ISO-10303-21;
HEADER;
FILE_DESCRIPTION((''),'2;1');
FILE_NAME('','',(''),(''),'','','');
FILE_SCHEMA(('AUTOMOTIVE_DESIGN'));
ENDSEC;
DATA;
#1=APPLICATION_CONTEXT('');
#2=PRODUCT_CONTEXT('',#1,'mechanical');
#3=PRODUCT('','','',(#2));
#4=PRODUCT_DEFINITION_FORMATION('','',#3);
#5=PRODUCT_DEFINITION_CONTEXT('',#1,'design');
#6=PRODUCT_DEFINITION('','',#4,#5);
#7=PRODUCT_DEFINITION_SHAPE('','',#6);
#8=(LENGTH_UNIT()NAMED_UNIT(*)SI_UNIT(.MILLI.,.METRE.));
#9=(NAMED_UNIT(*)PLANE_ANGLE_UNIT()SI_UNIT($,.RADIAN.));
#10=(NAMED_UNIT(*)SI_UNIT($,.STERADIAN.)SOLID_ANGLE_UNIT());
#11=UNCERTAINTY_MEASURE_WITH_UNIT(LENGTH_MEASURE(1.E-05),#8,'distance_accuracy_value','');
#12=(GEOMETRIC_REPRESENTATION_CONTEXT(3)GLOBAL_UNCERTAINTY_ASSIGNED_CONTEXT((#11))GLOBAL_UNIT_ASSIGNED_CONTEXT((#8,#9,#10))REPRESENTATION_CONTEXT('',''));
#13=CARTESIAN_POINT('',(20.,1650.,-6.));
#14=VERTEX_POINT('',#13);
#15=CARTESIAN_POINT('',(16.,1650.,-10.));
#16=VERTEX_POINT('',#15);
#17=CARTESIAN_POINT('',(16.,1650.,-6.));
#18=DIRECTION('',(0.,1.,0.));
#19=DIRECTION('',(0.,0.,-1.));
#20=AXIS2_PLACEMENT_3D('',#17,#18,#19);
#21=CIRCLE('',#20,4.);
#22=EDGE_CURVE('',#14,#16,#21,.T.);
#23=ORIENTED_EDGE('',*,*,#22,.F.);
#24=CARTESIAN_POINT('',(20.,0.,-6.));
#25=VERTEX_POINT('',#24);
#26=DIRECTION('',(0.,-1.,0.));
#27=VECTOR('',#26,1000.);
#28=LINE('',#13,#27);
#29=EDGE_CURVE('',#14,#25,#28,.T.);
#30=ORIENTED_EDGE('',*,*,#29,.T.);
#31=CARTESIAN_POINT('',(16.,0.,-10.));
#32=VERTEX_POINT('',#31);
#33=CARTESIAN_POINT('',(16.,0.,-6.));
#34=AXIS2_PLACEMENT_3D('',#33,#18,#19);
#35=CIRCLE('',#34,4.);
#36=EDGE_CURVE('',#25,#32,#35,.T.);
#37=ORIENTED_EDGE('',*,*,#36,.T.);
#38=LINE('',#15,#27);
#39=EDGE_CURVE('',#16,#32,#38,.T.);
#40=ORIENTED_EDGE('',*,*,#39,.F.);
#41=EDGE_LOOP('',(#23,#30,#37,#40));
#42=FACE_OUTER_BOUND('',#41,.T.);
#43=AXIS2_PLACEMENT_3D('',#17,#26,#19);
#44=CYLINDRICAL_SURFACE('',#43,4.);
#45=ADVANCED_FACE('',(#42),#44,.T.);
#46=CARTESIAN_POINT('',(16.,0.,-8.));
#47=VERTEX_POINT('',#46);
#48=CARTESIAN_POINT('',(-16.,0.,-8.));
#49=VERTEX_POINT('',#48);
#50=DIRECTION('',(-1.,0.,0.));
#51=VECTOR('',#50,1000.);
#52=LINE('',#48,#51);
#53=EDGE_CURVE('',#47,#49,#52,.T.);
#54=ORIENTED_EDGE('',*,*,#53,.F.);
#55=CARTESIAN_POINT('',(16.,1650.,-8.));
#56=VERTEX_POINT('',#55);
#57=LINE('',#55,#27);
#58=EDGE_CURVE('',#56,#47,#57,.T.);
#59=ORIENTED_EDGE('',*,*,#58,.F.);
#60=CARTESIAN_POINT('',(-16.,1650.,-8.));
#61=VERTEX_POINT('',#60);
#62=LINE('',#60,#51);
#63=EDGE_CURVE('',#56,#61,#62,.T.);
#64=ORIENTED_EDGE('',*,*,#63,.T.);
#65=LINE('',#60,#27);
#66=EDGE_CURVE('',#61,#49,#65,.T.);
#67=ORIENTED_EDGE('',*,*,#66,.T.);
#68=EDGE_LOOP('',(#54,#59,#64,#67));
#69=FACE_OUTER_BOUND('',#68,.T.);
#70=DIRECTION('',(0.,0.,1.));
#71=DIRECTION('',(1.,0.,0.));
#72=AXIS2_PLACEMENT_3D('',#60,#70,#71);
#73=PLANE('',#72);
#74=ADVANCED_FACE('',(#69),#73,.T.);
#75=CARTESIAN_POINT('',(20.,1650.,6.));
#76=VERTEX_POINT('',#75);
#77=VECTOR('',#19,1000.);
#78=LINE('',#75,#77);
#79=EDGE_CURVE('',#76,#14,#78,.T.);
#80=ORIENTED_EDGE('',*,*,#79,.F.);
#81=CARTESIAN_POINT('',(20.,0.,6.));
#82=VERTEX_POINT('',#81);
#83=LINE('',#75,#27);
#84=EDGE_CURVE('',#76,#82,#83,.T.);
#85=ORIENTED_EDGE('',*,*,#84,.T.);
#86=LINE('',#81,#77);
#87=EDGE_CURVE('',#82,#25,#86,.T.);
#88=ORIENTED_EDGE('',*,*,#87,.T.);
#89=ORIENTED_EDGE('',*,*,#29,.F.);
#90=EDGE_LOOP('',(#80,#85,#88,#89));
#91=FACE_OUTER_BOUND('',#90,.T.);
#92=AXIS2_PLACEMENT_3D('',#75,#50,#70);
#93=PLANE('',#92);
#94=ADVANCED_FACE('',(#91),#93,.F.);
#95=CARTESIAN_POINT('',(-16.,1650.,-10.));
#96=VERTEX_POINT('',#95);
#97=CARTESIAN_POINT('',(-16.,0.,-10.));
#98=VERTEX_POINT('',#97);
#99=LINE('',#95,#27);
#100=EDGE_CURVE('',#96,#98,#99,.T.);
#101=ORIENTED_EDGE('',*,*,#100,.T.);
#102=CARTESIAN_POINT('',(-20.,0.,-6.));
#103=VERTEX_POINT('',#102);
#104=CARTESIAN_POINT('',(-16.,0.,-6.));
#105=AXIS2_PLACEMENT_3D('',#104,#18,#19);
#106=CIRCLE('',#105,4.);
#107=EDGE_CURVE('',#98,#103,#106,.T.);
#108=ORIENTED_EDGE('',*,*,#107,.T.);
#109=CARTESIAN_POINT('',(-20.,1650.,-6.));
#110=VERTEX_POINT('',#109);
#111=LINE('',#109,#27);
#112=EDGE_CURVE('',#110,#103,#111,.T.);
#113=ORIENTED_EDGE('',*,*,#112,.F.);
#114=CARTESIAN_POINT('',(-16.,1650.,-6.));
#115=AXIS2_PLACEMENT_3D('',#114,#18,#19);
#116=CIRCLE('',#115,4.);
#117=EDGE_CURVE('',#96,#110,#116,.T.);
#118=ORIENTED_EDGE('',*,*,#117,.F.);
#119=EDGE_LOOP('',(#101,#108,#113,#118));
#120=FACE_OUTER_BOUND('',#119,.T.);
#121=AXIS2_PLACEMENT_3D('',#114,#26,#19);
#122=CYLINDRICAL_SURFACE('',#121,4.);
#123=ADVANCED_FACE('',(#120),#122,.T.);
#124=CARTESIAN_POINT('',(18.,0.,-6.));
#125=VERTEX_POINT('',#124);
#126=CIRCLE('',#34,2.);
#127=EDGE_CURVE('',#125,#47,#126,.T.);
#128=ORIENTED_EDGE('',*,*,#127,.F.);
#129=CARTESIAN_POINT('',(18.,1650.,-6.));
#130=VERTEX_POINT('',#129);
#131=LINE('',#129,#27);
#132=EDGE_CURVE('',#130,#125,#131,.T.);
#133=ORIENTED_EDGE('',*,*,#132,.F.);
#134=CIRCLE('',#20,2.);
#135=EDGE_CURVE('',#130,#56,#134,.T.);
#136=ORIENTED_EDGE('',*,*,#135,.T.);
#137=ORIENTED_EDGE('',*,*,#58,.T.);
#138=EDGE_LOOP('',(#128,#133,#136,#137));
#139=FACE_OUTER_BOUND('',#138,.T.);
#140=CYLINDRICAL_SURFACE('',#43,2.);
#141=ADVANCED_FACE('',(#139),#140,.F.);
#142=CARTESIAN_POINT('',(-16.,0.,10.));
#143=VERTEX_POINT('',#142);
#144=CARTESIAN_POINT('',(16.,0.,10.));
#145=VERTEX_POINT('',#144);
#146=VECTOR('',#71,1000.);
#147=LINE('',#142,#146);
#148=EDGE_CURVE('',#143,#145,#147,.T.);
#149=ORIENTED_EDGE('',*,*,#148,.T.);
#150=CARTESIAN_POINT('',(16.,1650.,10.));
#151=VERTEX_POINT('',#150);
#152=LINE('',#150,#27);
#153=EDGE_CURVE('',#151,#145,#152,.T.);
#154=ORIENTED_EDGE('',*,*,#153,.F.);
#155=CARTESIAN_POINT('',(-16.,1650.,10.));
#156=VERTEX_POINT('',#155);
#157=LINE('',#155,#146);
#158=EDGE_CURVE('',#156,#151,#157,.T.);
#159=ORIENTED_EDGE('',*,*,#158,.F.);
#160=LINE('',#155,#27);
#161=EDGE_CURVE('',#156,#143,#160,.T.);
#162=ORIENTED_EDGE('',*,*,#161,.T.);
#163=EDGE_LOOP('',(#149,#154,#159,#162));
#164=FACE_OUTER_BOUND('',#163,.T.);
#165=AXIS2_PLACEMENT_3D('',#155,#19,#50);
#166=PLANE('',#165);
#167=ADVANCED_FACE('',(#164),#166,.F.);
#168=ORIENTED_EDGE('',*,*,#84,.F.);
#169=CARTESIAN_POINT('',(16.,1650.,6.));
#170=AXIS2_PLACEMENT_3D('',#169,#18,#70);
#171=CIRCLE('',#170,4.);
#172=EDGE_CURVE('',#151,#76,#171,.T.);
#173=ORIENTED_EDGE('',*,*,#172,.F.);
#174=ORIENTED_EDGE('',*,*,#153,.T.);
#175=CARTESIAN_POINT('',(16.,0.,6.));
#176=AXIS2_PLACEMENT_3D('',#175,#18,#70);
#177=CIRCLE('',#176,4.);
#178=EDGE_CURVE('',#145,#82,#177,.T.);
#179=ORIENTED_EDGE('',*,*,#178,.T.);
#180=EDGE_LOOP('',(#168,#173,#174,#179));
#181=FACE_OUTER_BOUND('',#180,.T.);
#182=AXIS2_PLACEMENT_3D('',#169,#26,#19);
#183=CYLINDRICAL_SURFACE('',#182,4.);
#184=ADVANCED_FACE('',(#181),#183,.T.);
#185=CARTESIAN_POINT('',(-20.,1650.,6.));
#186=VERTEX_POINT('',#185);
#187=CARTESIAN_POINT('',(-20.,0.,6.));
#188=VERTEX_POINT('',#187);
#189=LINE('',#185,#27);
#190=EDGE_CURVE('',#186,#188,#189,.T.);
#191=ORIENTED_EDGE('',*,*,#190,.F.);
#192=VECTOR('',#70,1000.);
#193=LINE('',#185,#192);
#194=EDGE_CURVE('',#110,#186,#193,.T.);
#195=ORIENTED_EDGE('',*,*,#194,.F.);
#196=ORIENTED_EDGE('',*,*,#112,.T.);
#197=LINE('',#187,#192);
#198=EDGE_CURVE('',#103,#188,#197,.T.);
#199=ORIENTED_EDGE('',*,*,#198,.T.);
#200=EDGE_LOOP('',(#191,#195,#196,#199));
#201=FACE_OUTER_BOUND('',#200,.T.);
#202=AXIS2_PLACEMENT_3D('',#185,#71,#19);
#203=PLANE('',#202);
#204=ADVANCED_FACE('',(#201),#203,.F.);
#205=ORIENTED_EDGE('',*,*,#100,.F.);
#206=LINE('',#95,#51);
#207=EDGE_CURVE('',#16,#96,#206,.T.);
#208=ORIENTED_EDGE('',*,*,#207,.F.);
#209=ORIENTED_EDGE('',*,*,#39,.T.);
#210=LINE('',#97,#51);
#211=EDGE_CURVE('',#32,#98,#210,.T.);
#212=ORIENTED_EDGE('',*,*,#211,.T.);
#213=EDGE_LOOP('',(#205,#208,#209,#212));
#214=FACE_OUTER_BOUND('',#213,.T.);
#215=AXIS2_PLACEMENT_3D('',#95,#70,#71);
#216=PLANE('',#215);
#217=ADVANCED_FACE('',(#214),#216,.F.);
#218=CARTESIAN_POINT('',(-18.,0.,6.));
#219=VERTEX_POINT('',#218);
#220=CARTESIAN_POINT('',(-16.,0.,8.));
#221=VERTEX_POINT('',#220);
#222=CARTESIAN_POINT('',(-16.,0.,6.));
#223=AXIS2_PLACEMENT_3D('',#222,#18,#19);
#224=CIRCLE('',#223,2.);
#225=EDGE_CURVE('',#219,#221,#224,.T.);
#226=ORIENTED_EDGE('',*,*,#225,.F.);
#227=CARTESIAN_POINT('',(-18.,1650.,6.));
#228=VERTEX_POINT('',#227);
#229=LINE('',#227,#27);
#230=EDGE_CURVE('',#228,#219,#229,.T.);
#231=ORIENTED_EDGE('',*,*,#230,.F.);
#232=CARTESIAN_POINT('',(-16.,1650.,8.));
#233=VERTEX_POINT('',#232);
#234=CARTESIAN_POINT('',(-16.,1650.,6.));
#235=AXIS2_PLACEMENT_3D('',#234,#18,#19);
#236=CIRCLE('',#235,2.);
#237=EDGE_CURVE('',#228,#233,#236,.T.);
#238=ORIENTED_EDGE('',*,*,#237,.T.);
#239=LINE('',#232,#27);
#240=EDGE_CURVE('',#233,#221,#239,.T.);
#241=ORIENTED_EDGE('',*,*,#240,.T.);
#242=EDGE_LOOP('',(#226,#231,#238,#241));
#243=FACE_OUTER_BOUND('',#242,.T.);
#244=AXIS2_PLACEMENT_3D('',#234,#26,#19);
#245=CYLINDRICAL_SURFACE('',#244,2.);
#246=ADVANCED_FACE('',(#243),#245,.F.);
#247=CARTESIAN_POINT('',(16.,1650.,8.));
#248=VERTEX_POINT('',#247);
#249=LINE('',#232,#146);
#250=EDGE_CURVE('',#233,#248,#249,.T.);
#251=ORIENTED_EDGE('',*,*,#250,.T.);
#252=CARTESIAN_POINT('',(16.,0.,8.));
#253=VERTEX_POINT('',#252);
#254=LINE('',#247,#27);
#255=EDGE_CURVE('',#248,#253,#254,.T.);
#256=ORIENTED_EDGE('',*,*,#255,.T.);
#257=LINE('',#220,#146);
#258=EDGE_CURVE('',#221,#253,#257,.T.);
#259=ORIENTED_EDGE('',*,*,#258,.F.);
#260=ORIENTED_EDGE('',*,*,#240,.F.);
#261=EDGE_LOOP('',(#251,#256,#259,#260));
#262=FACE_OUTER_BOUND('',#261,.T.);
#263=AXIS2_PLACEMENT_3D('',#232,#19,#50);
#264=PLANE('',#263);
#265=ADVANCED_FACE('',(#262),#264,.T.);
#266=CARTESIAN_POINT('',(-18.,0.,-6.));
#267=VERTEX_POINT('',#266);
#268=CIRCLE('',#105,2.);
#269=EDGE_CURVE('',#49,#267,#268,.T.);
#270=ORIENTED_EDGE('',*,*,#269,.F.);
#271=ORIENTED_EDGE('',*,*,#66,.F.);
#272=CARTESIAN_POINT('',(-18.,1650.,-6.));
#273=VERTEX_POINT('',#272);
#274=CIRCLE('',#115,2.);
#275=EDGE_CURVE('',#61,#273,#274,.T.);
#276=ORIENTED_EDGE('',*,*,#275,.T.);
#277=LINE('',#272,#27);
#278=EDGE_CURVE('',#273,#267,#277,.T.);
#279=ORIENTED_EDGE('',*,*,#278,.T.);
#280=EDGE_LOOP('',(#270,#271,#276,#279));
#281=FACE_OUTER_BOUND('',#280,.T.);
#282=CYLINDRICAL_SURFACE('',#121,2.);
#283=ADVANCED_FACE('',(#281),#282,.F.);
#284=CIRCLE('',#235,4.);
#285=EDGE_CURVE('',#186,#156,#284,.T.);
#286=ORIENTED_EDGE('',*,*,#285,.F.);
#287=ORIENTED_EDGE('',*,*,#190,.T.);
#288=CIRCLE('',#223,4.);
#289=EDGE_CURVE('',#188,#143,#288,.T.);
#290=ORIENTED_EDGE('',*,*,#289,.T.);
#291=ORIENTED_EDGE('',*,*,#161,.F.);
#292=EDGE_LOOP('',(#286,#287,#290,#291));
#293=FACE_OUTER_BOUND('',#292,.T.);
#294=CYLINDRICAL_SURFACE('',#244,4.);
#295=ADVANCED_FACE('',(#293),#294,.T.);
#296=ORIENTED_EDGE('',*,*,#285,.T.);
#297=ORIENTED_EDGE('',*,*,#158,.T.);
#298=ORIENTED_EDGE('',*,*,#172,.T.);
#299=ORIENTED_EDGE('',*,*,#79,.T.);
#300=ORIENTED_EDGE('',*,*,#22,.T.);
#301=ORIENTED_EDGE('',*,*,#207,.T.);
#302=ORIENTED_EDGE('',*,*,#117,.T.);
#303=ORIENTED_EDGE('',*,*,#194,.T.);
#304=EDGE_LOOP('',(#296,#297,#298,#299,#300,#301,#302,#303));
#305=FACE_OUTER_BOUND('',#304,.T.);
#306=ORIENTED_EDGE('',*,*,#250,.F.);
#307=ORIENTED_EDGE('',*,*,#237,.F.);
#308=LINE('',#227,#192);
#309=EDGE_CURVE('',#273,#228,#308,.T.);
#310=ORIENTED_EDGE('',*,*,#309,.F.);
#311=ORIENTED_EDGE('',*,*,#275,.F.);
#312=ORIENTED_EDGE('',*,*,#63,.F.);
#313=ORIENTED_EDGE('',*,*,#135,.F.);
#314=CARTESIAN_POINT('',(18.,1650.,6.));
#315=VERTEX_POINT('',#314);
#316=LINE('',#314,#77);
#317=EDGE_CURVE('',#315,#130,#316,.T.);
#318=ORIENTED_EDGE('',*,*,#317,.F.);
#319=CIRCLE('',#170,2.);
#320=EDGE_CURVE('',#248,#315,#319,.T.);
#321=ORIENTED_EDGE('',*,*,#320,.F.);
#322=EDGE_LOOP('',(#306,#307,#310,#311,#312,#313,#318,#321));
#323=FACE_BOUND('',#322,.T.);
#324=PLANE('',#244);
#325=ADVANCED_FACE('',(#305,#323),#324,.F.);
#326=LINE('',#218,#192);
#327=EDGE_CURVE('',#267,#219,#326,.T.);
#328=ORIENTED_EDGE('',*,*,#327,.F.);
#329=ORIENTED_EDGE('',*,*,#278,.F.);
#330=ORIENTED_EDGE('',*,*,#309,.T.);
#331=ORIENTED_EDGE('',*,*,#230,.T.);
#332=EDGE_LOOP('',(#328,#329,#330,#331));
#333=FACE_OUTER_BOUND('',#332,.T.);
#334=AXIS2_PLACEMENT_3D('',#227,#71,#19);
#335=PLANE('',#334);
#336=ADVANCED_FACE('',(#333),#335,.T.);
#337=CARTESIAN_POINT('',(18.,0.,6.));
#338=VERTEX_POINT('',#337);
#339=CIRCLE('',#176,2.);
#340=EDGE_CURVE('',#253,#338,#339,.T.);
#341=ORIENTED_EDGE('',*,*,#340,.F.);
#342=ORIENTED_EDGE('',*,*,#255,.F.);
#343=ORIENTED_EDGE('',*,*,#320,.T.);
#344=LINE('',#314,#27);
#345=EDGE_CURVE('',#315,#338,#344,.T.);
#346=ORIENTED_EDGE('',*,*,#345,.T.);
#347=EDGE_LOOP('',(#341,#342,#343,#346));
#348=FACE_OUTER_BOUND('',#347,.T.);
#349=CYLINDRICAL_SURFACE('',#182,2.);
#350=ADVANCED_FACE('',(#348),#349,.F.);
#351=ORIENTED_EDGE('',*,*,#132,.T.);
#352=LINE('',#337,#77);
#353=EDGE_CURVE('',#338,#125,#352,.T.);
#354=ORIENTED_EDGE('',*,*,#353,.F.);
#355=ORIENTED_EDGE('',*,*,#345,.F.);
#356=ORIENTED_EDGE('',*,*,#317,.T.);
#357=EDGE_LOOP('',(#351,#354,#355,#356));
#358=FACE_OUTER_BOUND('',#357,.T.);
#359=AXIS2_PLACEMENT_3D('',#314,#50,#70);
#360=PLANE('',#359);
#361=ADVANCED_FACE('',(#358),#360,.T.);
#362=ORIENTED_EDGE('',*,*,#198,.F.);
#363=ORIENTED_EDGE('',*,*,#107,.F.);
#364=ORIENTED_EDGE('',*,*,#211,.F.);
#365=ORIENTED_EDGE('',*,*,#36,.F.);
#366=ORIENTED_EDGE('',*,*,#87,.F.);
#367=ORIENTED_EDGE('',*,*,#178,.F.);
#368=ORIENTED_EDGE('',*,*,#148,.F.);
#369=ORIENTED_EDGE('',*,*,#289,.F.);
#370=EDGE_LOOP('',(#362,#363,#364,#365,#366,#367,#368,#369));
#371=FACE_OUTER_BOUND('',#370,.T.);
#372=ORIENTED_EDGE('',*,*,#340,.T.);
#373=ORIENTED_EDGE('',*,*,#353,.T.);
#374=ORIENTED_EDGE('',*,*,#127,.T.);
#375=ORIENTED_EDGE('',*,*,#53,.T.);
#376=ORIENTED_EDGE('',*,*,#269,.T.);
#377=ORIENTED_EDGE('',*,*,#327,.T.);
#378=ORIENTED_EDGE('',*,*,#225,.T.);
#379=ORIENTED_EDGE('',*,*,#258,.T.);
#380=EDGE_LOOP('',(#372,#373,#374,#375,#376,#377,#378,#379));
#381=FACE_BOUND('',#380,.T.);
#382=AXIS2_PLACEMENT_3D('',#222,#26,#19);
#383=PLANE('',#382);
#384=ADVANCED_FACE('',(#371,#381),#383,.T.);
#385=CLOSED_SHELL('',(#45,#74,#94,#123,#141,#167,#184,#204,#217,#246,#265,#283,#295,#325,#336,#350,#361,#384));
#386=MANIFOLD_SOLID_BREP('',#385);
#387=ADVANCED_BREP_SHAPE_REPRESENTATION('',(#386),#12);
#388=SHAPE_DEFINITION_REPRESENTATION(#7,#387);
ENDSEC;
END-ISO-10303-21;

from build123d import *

# Parameters (mm, degrees)
EXTRUDE_1_DEPTH = 1650


with BuildPart() as part:
    # 草图1 → 凸台-拉伸1 (new body)
    with BuildSketch(Plane(origin=(0, 0, 0), x_dir=(1, 0, 0), z_dir=(0, 1, 0))):
        with BuildLine():
            Line((-16, -10), (16, -10))
            ThreePointArc((16, -10), (18.828427125, -8.828427125), (20, -6))
            Line((20, -6), (20, 6))
            ThreePointArc((20, 6), (18.828427125, 8.828427125), (16, 10))
            Line((16, 10), (-16, 10))
            ThreePointArc((-16, 10), (-18.828427125, 8.828427125), (-20, 6))
            Line((-20, 6), (-20, -6))
            ThreePointArc((-20, -6), (-18.828427125, -8.828427125), (-16, -10))
        make_face()
        with BuildLine():
            Line((-16, -8), (16, -8))
            ThreePointArc((16, -8), (17.414213562, -7.414213562), (18, -6))
            Line((18, -6), (18, 6))
            ThreePointArc((18, 6), (17.414213562, 7.414213562), (16, 8))
            Line((16, 8), (-16, 8))
            ThreePointArc((-16, 8), (-17.414213562, 7.414213562), (-18, 6))
            Line((-18, 6), (-18, -6))
            ThreePointArc((-18, -6), (-17.414213562, -7.414213562), (-16, -8))
        make_face(mode=Mode.SUBTRACT)
    extrude(amount=EXTRUDE_1_DEPTH)


solid = part.part
